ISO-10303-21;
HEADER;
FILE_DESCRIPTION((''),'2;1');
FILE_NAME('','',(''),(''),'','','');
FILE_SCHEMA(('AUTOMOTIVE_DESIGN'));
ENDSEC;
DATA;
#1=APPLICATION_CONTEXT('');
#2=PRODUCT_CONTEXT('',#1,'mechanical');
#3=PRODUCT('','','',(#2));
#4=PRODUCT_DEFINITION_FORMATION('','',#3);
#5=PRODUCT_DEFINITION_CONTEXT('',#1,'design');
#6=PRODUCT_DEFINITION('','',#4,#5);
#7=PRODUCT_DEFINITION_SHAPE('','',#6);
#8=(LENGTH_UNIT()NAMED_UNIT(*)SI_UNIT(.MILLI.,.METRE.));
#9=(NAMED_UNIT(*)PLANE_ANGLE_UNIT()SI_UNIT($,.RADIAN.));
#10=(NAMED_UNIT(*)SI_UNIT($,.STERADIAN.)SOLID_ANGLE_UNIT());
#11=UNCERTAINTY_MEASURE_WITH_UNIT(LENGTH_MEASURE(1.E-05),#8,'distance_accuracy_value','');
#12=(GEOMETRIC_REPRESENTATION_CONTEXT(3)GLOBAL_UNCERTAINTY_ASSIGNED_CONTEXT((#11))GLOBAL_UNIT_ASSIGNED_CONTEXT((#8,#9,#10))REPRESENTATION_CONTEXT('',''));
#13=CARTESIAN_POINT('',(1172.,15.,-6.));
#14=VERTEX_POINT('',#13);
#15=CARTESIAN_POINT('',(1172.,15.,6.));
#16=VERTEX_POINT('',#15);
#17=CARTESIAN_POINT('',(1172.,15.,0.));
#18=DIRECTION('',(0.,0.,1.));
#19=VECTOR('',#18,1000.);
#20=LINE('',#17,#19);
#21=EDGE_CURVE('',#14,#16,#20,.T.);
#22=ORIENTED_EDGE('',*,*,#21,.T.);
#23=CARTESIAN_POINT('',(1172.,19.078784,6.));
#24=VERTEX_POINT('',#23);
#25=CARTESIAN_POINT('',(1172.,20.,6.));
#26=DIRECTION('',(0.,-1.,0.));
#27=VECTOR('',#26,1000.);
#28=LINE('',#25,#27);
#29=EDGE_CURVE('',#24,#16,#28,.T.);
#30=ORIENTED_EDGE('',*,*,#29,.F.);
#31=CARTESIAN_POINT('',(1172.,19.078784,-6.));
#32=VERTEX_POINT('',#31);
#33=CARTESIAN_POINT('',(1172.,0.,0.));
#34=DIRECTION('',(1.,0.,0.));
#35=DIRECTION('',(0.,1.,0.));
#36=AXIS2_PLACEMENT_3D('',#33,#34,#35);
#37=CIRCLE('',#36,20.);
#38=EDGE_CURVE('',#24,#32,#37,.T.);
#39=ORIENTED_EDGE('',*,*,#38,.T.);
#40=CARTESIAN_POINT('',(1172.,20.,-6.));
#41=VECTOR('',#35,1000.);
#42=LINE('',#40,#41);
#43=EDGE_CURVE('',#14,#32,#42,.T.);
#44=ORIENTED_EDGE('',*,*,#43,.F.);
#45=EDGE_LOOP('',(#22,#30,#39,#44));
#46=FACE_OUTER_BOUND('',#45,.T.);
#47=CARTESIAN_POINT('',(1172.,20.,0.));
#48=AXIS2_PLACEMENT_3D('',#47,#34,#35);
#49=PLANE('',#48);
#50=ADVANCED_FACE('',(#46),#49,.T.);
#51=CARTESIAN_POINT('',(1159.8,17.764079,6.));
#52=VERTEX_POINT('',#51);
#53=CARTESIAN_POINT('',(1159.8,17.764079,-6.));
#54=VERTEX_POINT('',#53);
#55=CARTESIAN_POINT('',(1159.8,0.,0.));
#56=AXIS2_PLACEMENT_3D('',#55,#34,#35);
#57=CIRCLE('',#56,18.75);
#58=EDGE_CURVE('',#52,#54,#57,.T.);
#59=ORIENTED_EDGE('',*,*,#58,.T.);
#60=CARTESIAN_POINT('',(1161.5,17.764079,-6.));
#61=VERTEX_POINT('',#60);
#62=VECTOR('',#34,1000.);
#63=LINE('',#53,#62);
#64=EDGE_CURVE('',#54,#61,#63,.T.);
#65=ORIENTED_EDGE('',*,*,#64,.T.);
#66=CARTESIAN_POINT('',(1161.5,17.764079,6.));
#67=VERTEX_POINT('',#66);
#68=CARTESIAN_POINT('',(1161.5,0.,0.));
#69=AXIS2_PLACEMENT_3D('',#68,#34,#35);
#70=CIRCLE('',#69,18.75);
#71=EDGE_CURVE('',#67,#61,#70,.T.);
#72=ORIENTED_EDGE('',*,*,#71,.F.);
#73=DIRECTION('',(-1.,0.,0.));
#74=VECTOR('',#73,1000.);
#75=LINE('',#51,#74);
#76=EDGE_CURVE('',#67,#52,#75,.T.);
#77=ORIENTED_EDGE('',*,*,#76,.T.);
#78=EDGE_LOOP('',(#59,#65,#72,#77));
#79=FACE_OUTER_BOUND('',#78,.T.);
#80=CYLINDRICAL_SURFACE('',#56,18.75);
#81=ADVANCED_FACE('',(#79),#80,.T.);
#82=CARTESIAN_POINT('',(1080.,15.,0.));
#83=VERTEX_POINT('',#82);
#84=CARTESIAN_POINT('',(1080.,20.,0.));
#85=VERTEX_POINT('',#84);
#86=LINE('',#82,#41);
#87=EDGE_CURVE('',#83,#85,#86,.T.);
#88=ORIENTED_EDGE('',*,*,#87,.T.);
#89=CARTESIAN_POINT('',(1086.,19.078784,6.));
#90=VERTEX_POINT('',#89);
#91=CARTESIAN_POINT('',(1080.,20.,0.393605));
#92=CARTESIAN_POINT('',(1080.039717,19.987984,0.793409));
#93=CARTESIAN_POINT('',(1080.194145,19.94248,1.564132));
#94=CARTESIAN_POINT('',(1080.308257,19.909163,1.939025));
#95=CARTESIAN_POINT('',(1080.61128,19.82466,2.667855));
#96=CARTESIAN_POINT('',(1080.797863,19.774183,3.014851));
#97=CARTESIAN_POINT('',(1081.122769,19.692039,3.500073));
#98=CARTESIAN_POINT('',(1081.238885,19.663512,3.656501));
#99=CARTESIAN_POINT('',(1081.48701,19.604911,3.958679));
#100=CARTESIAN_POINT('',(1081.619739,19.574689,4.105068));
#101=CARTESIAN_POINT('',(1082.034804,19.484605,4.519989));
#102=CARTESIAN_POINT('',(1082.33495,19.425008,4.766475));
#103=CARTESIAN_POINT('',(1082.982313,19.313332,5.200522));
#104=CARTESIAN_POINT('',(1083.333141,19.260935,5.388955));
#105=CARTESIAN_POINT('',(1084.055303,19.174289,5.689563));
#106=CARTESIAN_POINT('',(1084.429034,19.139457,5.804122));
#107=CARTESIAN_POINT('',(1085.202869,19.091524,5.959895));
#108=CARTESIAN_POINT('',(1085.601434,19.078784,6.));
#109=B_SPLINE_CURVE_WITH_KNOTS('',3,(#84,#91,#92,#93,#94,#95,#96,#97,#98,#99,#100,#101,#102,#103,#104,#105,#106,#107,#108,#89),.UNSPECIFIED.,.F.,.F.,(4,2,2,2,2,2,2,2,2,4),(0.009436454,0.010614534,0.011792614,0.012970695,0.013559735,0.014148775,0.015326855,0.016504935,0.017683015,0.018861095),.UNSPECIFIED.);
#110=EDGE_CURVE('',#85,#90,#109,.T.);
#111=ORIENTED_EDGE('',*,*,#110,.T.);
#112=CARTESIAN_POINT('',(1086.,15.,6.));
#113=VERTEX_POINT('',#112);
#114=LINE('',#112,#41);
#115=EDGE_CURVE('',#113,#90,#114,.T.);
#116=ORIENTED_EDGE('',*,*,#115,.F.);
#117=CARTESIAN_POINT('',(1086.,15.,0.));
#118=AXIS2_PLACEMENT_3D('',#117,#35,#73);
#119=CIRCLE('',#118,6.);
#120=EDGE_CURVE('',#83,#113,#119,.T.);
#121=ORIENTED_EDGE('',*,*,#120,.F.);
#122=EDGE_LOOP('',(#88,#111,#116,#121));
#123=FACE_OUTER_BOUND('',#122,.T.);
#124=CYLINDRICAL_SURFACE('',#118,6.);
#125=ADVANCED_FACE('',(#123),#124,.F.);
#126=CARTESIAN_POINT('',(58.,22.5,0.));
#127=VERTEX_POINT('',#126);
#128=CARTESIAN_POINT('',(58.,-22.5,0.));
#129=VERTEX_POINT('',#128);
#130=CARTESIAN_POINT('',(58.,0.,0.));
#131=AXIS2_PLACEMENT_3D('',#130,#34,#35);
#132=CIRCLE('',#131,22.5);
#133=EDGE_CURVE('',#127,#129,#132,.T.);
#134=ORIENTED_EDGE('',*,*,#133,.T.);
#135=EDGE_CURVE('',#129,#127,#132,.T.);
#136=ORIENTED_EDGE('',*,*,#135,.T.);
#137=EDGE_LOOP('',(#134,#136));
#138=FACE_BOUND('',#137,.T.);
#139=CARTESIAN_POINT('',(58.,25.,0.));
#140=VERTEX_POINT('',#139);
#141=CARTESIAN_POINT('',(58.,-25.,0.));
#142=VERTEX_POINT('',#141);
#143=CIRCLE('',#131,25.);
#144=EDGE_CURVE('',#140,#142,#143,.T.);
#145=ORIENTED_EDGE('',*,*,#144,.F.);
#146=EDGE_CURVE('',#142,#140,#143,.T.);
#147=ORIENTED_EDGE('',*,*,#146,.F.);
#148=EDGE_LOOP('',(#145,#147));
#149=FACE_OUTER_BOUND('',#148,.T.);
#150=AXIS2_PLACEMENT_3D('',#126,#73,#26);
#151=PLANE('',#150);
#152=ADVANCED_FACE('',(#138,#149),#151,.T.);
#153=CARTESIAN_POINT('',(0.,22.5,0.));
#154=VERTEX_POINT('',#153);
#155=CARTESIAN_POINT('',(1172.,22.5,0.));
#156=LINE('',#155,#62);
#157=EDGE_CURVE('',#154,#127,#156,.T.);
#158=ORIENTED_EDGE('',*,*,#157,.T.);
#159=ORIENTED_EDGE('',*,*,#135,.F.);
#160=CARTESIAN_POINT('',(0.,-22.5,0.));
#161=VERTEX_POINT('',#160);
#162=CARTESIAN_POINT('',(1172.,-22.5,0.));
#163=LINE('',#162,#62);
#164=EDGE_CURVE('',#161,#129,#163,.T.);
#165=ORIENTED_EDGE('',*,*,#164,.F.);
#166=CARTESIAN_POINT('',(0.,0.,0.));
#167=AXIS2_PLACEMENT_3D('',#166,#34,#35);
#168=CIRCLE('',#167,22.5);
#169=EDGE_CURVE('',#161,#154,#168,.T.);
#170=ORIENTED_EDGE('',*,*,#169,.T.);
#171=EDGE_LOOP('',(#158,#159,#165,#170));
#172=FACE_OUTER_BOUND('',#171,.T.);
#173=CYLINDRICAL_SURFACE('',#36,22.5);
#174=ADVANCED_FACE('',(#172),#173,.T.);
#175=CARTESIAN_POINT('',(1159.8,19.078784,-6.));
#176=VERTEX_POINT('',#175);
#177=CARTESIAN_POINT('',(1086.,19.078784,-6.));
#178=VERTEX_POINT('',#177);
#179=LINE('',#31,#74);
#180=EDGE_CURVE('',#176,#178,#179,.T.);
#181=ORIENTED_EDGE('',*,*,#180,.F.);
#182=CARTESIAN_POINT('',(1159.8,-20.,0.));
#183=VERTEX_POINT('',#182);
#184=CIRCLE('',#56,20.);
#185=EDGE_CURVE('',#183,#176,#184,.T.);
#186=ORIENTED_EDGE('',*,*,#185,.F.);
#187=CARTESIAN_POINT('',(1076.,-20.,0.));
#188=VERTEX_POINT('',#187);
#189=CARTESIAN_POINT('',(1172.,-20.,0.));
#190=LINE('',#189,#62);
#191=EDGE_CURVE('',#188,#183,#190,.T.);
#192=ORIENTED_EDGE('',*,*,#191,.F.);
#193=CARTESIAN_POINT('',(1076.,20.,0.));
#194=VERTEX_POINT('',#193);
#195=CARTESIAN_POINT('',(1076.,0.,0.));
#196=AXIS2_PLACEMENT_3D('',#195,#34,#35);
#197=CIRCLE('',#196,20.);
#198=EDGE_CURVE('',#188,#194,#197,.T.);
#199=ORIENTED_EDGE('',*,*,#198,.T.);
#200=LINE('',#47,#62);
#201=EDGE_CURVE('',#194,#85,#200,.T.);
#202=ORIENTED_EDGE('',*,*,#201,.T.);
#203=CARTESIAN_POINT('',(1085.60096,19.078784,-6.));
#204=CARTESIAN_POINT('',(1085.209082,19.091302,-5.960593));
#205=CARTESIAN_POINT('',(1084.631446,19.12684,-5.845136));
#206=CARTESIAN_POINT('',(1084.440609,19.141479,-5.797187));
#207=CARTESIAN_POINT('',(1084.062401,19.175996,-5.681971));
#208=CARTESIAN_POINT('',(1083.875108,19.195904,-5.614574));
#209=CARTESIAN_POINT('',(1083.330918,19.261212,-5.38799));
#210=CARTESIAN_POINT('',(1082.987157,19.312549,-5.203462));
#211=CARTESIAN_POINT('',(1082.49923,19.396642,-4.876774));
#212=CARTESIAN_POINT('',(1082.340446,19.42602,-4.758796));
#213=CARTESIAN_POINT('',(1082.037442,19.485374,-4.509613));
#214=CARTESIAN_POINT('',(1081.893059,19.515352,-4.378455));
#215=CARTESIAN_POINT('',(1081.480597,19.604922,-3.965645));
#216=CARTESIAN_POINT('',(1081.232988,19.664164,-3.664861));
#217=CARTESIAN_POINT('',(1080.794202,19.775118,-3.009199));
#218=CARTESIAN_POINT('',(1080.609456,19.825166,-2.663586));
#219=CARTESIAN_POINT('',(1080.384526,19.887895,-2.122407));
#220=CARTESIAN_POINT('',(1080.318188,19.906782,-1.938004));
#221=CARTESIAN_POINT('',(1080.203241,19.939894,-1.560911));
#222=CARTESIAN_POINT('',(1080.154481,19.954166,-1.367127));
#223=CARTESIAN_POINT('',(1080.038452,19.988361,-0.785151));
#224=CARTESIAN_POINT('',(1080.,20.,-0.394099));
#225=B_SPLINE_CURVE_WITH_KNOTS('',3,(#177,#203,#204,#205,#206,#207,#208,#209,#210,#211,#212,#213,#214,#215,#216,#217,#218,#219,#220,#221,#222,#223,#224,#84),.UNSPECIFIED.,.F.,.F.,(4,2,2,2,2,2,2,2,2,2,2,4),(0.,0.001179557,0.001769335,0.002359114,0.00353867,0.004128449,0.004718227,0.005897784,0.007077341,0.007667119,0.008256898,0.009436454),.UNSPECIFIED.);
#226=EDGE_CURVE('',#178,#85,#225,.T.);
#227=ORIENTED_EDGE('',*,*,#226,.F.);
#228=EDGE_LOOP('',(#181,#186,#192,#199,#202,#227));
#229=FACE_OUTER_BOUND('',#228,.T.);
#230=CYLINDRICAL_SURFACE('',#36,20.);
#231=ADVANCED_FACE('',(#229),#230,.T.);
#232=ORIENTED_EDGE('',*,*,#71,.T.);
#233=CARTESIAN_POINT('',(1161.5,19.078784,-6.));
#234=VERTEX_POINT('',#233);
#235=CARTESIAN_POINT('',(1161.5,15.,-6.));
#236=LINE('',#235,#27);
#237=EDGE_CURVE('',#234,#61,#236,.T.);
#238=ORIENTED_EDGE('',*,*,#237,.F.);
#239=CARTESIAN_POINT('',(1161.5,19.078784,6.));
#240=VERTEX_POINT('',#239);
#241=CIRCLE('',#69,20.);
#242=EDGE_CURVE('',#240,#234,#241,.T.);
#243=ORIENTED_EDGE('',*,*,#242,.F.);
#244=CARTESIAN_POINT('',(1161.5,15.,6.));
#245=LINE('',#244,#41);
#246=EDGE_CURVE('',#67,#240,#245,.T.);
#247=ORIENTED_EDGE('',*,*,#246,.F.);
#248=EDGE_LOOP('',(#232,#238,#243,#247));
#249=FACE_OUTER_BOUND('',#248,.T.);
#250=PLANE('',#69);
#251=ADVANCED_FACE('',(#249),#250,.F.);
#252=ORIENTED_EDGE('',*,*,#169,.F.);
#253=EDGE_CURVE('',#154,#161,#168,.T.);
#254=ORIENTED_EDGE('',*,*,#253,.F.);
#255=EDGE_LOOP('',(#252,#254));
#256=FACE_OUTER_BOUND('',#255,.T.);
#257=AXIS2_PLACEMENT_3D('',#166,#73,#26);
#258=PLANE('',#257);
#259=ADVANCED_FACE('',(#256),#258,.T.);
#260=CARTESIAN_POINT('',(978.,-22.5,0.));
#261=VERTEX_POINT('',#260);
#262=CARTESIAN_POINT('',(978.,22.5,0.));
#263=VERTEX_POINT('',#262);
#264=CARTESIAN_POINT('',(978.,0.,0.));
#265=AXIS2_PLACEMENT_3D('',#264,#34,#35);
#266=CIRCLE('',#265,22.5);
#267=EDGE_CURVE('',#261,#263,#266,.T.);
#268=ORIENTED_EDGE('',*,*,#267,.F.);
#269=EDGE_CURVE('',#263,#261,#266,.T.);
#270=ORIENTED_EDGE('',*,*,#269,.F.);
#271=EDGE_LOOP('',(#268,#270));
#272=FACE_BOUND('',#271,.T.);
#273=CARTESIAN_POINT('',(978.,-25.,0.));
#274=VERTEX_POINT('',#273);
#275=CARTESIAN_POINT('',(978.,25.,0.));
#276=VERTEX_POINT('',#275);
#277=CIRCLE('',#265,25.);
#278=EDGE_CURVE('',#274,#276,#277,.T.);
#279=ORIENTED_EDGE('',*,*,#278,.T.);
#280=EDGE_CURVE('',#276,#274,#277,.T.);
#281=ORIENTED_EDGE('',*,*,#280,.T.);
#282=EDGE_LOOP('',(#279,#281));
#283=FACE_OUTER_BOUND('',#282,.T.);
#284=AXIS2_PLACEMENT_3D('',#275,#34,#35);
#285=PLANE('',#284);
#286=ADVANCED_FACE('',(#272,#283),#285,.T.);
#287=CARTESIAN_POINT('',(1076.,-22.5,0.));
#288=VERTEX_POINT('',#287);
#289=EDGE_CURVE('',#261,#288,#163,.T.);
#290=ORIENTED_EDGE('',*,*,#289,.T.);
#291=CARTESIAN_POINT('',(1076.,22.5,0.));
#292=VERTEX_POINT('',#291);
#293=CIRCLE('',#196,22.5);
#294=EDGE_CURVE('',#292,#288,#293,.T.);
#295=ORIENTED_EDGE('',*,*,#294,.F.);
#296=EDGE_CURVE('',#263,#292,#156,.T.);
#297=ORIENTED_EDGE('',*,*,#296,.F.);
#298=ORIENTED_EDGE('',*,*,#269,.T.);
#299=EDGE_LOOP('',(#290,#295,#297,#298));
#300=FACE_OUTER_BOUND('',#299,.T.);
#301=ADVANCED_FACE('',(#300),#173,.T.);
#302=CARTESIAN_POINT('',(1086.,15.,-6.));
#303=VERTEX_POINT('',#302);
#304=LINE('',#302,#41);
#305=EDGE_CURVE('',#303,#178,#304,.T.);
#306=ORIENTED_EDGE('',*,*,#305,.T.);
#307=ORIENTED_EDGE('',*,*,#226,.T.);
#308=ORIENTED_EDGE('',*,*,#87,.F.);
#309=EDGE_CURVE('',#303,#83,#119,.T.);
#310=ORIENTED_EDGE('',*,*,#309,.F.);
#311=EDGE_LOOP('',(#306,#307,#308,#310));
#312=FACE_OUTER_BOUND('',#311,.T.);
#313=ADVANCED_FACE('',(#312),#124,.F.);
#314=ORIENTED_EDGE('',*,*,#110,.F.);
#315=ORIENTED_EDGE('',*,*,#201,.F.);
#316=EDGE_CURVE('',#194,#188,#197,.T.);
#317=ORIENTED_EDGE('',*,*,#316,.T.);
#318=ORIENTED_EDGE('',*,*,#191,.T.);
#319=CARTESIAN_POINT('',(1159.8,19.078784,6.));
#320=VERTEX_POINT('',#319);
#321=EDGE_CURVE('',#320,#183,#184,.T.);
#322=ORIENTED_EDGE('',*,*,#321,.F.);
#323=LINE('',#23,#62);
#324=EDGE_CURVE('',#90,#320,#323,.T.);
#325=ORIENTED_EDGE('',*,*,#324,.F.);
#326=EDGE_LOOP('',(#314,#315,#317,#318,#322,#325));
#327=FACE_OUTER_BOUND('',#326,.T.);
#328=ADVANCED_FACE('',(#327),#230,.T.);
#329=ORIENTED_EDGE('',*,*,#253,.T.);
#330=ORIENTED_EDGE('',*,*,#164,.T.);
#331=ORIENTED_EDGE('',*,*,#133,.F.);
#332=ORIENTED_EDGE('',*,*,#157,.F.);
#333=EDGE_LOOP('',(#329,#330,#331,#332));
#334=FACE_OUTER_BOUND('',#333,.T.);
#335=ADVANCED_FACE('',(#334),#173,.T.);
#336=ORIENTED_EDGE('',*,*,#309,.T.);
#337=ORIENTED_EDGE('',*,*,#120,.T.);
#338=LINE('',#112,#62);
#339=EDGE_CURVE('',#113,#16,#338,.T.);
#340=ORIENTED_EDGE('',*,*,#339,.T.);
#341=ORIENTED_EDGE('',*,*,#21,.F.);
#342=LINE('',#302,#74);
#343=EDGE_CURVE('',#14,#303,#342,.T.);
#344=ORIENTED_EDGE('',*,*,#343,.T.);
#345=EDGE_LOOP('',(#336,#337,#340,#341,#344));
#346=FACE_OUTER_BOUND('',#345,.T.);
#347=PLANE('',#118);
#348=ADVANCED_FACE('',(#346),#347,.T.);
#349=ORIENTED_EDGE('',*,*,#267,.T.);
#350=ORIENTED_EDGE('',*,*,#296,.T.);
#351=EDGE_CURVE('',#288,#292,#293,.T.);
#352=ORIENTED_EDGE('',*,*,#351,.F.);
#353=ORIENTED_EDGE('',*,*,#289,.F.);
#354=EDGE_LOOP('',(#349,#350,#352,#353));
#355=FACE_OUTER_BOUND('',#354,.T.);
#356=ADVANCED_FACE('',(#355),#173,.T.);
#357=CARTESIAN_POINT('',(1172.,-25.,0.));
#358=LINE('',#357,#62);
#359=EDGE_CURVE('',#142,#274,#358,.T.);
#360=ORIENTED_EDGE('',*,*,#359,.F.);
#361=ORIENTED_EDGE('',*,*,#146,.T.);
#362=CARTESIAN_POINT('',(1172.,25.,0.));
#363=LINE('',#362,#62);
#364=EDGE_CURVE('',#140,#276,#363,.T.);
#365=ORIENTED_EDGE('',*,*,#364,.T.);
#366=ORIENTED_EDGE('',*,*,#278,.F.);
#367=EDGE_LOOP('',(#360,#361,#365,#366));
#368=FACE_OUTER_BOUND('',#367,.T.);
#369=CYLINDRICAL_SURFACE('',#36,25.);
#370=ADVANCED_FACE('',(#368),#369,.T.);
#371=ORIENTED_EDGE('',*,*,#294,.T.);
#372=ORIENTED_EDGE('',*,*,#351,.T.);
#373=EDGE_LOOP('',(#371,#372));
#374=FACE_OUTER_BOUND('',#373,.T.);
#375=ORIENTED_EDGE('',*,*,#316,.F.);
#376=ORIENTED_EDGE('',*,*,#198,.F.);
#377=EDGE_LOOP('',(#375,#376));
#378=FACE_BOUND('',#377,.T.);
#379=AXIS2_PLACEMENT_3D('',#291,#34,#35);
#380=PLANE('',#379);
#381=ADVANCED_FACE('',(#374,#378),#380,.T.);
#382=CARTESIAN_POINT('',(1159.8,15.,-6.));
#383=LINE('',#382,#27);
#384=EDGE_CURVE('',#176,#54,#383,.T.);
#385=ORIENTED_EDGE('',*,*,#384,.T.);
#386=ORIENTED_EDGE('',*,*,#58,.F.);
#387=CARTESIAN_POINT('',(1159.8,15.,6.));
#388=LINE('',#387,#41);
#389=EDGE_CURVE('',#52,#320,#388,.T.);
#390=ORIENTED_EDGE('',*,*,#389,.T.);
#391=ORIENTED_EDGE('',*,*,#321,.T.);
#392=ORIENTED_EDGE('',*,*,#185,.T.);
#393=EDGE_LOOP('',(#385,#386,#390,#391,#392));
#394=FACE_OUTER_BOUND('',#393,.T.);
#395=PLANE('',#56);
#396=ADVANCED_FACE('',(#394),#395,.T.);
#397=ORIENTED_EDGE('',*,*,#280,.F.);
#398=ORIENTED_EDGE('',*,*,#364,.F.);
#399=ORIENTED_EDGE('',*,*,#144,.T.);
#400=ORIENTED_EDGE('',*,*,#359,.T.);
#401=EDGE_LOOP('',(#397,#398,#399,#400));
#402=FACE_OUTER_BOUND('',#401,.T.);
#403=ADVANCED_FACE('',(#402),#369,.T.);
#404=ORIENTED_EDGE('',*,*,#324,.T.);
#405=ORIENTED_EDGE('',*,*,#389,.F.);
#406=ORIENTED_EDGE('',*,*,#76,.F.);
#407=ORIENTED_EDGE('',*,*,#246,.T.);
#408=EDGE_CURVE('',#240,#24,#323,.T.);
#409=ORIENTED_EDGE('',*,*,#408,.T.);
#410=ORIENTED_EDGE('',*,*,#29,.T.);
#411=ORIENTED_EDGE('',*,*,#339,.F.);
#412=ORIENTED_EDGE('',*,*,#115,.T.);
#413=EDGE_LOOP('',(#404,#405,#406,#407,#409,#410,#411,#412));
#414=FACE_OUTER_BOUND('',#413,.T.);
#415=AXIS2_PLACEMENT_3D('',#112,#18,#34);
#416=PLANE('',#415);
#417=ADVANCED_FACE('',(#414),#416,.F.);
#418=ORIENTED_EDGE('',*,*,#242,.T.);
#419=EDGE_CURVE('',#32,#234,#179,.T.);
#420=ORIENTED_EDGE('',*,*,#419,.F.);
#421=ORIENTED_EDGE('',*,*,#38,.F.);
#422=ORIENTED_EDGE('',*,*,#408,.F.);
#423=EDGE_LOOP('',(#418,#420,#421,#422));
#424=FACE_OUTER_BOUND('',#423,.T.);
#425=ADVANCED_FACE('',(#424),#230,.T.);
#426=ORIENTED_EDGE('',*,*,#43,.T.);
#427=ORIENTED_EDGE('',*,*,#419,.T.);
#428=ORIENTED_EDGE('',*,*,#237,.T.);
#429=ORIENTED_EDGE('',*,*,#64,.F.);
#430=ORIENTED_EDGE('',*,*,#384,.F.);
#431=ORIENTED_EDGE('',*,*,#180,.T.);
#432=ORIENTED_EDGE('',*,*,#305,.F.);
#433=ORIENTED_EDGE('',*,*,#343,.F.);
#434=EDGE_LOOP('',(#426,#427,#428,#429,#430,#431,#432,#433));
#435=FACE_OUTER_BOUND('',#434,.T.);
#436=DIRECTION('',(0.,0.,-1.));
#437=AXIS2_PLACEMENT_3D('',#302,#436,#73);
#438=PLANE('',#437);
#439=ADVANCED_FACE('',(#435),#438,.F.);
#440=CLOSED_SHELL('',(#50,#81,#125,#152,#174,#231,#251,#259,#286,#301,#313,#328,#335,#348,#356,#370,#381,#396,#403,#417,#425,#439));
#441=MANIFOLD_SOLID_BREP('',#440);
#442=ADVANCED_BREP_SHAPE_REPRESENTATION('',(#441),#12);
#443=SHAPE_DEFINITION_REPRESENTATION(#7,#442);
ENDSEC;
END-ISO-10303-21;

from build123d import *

# Parameters (mm, degrees)
CUT_EXTRUDE_1_DEPTH = 5
SKETCH_3_R          = 20
SKETCH_3_R_2        = 18.75
CUT_EXTRUDE_2_DEPTH = 1.7


with BuildPart() as part:
    # 草图1 → 旋转1 (revolve)
    with BuildSketch(Plane.XY):
        Polygon((0, 0), (0, 22.5), (58, 22.5), (58, 25), (978, 25), (978, 22.5), (1076, 22.5), (1076, 20), (1172, 20), (1172, 0), align=None)
    revolve(axis=Axis((1172, 0, 0), (-1, 0, 0)))

    # 草图2 → 切除-拉伸1 (cut)
    with BuildSketch(Plane(origin=(0, 20, 0), x_dir=(1, 0, 0), z_dir=(0, 1, 0))):
        with BuildLine():
            Line((1086, 6), (1182, 6))
            Line((1182, 6), (1182, -6))
            Line((1182, -6), (1086, -6))
            ThreePointArc((1086, -6), (1080, 0), (1086, 6))
        make_face()
    extrude(amount=-CUT_EXTRUDE_1_DEPTH, mode=Mode.SUBTRACT)

    # 草图3 → 切除-拉伸2 (cut)
    with BuildSketch(Plane(origin=(1161.5, 0, 0), x_dir=(0, 0, -1), z_dir=(1, 0, 0))):
        with Locations(Location((0, 0, 0), (0, 0, 90))):
            Circle(SKETCH_3_R)
        Circle(SKETCH_3_R_2, mode=Mode.SUBTRACT)
    extrude(amount=-CUT_EXTRUDE_2_DEPTH, mode=Mode.SUBTRACT)


solid = part.part
